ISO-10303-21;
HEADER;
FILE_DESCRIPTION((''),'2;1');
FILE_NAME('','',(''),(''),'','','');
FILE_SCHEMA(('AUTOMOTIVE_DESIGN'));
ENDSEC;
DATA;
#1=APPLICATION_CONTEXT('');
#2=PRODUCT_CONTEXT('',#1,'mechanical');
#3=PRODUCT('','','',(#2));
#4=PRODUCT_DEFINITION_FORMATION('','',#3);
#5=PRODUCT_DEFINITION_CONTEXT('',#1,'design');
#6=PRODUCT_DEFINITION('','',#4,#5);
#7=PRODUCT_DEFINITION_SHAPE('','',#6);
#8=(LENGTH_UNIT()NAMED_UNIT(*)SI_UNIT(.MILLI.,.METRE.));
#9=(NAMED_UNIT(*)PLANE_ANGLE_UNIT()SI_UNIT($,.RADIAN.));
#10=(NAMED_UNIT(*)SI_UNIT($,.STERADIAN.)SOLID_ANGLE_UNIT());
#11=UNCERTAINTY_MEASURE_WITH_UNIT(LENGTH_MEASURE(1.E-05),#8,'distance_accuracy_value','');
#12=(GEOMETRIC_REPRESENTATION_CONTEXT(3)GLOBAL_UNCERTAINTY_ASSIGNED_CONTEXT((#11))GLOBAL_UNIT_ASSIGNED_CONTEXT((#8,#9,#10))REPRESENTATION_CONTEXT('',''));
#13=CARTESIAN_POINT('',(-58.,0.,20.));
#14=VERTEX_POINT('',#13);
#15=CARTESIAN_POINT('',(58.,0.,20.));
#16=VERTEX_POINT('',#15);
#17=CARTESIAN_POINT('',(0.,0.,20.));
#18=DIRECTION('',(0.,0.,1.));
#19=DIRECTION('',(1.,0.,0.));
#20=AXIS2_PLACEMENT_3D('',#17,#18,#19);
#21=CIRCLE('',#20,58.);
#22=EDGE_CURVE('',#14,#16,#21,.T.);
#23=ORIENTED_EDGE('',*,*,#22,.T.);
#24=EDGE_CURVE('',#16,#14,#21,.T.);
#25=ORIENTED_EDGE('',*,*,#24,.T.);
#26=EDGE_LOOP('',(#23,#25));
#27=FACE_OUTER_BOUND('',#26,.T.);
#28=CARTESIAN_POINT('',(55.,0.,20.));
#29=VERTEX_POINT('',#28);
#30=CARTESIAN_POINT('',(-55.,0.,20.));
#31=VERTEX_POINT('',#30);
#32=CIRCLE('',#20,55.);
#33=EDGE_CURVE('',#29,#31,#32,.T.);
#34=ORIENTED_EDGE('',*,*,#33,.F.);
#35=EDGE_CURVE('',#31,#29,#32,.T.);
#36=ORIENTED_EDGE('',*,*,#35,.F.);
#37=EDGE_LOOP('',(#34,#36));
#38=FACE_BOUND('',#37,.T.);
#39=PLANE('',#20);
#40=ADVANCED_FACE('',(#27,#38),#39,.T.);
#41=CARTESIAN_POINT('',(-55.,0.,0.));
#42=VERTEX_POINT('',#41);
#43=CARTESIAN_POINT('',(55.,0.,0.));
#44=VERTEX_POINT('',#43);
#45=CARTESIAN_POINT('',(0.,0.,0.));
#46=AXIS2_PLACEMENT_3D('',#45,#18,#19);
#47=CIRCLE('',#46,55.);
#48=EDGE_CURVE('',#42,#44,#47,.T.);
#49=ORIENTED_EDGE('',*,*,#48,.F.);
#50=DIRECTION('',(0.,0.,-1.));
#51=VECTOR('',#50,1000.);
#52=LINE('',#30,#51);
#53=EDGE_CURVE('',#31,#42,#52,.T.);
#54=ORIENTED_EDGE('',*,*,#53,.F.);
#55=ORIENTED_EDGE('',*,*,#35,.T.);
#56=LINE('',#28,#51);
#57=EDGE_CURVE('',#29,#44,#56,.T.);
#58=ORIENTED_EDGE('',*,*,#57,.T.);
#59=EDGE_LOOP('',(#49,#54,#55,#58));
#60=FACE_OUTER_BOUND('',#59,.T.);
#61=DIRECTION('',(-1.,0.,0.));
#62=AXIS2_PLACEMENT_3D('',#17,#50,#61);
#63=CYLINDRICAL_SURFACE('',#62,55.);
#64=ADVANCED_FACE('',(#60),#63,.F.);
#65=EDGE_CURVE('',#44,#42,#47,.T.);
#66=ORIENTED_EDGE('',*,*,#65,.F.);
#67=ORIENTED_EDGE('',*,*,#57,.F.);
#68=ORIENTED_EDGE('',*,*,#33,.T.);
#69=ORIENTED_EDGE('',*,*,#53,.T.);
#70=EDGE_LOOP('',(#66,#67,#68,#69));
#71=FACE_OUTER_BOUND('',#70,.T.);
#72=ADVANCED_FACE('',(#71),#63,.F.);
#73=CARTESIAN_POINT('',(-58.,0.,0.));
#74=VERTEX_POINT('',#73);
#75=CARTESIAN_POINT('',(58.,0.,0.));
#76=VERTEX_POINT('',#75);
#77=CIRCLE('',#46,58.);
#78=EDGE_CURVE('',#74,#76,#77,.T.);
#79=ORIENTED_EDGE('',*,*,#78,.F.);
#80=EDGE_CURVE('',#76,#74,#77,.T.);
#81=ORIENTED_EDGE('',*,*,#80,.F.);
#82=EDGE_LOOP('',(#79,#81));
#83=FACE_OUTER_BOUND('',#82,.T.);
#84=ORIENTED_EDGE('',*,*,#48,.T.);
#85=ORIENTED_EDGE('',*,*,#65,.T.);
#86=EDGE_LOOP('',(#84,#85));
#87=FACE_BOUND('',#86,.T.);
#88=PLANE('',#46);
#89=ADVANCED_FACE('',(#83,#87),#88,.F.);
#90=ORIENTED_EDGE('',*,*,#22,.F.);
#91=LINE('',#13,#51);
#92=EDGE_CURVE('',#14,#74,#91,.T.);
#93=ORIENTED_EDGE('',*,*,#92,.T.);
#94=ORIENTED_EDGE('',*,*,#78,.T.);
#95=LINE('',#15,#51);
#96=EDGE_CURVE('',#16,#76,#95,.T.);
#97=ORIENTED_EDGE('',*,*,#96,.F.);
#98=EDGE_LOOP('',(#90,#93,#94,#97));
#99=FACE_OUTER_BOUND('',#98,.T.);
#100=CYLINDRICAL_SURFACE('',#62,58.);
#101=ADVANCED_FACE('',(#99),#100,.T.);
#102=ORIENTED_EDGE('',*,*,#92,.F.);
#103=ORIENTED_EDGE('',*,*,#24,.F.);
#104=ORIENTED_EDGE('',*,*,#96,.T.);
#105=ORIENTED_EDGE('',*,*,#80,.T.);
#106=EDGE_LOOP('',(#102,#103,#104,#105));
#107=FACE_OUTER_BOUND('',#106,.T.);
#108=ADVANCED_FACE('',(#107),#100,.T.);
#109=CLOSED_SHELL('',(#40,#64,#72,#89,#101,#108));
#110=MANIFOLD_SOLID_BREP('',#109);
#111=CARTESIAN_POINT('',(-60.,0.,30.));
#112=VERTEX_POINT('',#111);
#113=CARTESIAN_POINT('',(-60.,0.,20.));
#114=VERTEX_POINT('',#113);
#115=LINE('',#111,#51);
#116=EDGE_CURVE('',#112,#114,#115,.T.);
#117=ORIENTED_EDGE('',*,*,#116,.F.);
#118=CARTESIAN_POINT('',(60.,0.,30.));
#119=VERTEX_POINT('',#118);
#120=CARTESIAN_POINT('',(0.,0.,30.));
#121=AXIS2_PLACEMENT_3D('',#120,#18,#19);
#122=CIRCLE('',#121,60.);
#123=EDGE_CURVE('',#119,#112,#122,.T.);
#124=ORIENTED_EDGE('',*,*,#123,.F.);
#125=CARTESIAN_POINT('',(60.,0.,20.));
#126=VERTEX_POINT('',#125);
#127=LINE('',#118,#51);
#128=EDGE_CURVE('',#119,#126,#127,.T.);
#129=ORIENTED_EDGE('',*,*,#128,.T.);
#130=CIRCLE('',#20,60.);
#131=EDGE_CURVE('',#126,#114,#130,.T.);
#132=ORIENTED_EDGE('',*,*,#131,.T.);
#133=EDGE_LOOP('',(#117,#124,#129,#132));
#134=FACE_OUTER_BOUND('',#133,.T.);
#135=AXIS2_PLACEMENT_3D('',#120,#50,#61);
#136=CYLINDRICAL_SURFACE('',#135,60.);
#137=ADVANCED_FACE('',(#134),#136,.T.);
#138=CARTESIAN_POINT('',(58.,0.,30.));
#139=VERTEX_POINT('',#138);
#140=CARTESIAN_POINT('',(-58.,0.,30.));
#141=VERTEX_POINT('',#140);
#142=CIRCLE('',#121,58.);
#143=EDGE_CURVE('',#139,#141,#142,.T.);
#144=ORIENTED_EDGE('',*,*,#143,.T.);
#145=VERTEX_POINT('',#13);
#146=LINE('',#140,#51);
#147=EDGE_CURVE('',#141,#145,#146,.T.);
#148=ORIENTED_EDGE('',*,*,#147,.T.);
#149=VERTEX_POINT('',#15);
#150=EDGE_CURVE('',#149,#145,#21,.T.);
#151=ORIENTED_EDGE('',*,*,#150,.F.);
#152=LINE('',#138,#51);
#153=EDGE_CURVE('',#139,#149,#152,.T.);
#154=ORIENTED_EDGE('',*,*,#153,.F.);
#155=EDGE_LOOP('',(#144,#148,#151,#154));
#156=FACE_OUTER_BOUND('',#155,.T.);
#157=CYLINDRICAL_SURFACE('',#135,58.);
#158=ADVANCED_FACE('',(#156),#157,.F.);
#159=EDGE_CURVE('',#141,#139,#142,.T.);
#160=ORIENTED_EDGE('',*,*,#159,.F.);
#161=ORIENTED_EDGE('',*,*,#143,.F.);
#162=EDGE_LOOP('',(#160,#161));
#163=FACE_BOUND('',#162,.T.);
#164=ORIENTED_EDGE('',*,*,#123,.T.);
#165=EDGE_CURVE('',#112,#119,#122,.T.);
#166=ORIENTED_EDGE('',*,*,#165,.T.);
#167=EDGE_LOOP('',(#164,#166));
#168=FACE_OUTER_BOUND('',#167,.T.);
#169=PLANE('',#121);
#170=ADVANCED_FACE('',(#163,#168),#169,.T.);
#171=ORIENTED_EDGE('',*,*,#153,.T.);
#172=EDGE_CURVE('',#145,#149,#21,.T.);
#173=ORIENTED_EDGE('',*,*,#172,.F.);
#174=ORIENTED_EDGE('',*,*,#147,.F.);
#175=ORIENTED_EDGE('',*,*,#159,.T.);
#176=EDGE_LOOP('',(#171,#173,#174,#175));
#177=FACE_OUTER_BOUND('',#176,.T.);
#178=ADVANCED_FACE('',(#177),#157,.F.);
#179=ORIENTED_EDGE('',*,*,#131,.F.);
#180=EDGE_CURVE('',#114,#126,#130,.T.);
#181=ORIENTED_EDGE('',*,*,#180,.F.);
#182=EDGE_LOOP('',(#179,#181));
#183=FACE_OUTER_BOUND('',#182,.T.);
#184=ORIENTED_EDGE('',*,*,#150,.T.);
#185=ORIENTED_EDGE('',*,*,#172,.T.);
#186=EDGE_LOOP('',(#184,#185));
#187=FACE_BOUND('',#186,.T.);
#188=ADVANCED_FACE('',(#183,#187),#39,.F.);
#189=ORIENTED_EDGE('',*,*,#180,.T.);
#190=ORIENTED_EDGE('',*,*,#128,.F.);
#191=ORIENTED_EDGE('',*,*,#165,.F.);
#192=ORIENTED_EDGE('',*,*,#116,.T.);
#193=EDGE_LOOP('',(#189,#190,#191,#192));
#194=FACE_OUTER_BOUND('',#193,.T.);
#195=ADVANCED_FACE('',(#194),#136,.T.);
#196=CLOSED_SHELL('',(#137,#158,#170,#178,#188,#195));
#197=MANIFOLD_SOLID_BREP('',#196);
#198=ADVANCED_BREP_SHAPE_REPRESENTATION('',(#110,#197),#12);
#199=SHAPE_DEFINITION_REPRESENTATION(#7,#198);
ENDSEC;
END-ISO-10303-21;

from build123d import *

# Parameters (mm, degrees)
SKETCH1_R           = 58
SKETCH1_R_2         = 55
BOSS_EXTRUDE1_DEPTH = 20
SKETCH2_R           = 60
SKETCH2_R_2         = 58
BOSS_EXTRUDE2_DEPTH = 10


with BuildPart() as part:
    # Sketch1 → Boss-Extrude1 (new body)
    with BuildSketch(Plane.XY):
        Circle(SKETCH1_R)
        Circle(SKETCH1_R_2, mode=Mode.SUBTRACT)
    extrude(amount=BOSS_EXTRUDE1_DEPTH)


with BuildPart() as body_2:
    # Sketch2 → Boss-Extrude2 (new body)
    with BuildSketch(Plane.XY.offset(20)):
        Circle(SKETCH2_R)
        Circle(SKETCH2_R_2, mode=Mode.SUBTRACT)
    extrude(amount=BOSS_EXTRUDE2_DEPTH)


solid = Compound([part.part, body_2.part])
